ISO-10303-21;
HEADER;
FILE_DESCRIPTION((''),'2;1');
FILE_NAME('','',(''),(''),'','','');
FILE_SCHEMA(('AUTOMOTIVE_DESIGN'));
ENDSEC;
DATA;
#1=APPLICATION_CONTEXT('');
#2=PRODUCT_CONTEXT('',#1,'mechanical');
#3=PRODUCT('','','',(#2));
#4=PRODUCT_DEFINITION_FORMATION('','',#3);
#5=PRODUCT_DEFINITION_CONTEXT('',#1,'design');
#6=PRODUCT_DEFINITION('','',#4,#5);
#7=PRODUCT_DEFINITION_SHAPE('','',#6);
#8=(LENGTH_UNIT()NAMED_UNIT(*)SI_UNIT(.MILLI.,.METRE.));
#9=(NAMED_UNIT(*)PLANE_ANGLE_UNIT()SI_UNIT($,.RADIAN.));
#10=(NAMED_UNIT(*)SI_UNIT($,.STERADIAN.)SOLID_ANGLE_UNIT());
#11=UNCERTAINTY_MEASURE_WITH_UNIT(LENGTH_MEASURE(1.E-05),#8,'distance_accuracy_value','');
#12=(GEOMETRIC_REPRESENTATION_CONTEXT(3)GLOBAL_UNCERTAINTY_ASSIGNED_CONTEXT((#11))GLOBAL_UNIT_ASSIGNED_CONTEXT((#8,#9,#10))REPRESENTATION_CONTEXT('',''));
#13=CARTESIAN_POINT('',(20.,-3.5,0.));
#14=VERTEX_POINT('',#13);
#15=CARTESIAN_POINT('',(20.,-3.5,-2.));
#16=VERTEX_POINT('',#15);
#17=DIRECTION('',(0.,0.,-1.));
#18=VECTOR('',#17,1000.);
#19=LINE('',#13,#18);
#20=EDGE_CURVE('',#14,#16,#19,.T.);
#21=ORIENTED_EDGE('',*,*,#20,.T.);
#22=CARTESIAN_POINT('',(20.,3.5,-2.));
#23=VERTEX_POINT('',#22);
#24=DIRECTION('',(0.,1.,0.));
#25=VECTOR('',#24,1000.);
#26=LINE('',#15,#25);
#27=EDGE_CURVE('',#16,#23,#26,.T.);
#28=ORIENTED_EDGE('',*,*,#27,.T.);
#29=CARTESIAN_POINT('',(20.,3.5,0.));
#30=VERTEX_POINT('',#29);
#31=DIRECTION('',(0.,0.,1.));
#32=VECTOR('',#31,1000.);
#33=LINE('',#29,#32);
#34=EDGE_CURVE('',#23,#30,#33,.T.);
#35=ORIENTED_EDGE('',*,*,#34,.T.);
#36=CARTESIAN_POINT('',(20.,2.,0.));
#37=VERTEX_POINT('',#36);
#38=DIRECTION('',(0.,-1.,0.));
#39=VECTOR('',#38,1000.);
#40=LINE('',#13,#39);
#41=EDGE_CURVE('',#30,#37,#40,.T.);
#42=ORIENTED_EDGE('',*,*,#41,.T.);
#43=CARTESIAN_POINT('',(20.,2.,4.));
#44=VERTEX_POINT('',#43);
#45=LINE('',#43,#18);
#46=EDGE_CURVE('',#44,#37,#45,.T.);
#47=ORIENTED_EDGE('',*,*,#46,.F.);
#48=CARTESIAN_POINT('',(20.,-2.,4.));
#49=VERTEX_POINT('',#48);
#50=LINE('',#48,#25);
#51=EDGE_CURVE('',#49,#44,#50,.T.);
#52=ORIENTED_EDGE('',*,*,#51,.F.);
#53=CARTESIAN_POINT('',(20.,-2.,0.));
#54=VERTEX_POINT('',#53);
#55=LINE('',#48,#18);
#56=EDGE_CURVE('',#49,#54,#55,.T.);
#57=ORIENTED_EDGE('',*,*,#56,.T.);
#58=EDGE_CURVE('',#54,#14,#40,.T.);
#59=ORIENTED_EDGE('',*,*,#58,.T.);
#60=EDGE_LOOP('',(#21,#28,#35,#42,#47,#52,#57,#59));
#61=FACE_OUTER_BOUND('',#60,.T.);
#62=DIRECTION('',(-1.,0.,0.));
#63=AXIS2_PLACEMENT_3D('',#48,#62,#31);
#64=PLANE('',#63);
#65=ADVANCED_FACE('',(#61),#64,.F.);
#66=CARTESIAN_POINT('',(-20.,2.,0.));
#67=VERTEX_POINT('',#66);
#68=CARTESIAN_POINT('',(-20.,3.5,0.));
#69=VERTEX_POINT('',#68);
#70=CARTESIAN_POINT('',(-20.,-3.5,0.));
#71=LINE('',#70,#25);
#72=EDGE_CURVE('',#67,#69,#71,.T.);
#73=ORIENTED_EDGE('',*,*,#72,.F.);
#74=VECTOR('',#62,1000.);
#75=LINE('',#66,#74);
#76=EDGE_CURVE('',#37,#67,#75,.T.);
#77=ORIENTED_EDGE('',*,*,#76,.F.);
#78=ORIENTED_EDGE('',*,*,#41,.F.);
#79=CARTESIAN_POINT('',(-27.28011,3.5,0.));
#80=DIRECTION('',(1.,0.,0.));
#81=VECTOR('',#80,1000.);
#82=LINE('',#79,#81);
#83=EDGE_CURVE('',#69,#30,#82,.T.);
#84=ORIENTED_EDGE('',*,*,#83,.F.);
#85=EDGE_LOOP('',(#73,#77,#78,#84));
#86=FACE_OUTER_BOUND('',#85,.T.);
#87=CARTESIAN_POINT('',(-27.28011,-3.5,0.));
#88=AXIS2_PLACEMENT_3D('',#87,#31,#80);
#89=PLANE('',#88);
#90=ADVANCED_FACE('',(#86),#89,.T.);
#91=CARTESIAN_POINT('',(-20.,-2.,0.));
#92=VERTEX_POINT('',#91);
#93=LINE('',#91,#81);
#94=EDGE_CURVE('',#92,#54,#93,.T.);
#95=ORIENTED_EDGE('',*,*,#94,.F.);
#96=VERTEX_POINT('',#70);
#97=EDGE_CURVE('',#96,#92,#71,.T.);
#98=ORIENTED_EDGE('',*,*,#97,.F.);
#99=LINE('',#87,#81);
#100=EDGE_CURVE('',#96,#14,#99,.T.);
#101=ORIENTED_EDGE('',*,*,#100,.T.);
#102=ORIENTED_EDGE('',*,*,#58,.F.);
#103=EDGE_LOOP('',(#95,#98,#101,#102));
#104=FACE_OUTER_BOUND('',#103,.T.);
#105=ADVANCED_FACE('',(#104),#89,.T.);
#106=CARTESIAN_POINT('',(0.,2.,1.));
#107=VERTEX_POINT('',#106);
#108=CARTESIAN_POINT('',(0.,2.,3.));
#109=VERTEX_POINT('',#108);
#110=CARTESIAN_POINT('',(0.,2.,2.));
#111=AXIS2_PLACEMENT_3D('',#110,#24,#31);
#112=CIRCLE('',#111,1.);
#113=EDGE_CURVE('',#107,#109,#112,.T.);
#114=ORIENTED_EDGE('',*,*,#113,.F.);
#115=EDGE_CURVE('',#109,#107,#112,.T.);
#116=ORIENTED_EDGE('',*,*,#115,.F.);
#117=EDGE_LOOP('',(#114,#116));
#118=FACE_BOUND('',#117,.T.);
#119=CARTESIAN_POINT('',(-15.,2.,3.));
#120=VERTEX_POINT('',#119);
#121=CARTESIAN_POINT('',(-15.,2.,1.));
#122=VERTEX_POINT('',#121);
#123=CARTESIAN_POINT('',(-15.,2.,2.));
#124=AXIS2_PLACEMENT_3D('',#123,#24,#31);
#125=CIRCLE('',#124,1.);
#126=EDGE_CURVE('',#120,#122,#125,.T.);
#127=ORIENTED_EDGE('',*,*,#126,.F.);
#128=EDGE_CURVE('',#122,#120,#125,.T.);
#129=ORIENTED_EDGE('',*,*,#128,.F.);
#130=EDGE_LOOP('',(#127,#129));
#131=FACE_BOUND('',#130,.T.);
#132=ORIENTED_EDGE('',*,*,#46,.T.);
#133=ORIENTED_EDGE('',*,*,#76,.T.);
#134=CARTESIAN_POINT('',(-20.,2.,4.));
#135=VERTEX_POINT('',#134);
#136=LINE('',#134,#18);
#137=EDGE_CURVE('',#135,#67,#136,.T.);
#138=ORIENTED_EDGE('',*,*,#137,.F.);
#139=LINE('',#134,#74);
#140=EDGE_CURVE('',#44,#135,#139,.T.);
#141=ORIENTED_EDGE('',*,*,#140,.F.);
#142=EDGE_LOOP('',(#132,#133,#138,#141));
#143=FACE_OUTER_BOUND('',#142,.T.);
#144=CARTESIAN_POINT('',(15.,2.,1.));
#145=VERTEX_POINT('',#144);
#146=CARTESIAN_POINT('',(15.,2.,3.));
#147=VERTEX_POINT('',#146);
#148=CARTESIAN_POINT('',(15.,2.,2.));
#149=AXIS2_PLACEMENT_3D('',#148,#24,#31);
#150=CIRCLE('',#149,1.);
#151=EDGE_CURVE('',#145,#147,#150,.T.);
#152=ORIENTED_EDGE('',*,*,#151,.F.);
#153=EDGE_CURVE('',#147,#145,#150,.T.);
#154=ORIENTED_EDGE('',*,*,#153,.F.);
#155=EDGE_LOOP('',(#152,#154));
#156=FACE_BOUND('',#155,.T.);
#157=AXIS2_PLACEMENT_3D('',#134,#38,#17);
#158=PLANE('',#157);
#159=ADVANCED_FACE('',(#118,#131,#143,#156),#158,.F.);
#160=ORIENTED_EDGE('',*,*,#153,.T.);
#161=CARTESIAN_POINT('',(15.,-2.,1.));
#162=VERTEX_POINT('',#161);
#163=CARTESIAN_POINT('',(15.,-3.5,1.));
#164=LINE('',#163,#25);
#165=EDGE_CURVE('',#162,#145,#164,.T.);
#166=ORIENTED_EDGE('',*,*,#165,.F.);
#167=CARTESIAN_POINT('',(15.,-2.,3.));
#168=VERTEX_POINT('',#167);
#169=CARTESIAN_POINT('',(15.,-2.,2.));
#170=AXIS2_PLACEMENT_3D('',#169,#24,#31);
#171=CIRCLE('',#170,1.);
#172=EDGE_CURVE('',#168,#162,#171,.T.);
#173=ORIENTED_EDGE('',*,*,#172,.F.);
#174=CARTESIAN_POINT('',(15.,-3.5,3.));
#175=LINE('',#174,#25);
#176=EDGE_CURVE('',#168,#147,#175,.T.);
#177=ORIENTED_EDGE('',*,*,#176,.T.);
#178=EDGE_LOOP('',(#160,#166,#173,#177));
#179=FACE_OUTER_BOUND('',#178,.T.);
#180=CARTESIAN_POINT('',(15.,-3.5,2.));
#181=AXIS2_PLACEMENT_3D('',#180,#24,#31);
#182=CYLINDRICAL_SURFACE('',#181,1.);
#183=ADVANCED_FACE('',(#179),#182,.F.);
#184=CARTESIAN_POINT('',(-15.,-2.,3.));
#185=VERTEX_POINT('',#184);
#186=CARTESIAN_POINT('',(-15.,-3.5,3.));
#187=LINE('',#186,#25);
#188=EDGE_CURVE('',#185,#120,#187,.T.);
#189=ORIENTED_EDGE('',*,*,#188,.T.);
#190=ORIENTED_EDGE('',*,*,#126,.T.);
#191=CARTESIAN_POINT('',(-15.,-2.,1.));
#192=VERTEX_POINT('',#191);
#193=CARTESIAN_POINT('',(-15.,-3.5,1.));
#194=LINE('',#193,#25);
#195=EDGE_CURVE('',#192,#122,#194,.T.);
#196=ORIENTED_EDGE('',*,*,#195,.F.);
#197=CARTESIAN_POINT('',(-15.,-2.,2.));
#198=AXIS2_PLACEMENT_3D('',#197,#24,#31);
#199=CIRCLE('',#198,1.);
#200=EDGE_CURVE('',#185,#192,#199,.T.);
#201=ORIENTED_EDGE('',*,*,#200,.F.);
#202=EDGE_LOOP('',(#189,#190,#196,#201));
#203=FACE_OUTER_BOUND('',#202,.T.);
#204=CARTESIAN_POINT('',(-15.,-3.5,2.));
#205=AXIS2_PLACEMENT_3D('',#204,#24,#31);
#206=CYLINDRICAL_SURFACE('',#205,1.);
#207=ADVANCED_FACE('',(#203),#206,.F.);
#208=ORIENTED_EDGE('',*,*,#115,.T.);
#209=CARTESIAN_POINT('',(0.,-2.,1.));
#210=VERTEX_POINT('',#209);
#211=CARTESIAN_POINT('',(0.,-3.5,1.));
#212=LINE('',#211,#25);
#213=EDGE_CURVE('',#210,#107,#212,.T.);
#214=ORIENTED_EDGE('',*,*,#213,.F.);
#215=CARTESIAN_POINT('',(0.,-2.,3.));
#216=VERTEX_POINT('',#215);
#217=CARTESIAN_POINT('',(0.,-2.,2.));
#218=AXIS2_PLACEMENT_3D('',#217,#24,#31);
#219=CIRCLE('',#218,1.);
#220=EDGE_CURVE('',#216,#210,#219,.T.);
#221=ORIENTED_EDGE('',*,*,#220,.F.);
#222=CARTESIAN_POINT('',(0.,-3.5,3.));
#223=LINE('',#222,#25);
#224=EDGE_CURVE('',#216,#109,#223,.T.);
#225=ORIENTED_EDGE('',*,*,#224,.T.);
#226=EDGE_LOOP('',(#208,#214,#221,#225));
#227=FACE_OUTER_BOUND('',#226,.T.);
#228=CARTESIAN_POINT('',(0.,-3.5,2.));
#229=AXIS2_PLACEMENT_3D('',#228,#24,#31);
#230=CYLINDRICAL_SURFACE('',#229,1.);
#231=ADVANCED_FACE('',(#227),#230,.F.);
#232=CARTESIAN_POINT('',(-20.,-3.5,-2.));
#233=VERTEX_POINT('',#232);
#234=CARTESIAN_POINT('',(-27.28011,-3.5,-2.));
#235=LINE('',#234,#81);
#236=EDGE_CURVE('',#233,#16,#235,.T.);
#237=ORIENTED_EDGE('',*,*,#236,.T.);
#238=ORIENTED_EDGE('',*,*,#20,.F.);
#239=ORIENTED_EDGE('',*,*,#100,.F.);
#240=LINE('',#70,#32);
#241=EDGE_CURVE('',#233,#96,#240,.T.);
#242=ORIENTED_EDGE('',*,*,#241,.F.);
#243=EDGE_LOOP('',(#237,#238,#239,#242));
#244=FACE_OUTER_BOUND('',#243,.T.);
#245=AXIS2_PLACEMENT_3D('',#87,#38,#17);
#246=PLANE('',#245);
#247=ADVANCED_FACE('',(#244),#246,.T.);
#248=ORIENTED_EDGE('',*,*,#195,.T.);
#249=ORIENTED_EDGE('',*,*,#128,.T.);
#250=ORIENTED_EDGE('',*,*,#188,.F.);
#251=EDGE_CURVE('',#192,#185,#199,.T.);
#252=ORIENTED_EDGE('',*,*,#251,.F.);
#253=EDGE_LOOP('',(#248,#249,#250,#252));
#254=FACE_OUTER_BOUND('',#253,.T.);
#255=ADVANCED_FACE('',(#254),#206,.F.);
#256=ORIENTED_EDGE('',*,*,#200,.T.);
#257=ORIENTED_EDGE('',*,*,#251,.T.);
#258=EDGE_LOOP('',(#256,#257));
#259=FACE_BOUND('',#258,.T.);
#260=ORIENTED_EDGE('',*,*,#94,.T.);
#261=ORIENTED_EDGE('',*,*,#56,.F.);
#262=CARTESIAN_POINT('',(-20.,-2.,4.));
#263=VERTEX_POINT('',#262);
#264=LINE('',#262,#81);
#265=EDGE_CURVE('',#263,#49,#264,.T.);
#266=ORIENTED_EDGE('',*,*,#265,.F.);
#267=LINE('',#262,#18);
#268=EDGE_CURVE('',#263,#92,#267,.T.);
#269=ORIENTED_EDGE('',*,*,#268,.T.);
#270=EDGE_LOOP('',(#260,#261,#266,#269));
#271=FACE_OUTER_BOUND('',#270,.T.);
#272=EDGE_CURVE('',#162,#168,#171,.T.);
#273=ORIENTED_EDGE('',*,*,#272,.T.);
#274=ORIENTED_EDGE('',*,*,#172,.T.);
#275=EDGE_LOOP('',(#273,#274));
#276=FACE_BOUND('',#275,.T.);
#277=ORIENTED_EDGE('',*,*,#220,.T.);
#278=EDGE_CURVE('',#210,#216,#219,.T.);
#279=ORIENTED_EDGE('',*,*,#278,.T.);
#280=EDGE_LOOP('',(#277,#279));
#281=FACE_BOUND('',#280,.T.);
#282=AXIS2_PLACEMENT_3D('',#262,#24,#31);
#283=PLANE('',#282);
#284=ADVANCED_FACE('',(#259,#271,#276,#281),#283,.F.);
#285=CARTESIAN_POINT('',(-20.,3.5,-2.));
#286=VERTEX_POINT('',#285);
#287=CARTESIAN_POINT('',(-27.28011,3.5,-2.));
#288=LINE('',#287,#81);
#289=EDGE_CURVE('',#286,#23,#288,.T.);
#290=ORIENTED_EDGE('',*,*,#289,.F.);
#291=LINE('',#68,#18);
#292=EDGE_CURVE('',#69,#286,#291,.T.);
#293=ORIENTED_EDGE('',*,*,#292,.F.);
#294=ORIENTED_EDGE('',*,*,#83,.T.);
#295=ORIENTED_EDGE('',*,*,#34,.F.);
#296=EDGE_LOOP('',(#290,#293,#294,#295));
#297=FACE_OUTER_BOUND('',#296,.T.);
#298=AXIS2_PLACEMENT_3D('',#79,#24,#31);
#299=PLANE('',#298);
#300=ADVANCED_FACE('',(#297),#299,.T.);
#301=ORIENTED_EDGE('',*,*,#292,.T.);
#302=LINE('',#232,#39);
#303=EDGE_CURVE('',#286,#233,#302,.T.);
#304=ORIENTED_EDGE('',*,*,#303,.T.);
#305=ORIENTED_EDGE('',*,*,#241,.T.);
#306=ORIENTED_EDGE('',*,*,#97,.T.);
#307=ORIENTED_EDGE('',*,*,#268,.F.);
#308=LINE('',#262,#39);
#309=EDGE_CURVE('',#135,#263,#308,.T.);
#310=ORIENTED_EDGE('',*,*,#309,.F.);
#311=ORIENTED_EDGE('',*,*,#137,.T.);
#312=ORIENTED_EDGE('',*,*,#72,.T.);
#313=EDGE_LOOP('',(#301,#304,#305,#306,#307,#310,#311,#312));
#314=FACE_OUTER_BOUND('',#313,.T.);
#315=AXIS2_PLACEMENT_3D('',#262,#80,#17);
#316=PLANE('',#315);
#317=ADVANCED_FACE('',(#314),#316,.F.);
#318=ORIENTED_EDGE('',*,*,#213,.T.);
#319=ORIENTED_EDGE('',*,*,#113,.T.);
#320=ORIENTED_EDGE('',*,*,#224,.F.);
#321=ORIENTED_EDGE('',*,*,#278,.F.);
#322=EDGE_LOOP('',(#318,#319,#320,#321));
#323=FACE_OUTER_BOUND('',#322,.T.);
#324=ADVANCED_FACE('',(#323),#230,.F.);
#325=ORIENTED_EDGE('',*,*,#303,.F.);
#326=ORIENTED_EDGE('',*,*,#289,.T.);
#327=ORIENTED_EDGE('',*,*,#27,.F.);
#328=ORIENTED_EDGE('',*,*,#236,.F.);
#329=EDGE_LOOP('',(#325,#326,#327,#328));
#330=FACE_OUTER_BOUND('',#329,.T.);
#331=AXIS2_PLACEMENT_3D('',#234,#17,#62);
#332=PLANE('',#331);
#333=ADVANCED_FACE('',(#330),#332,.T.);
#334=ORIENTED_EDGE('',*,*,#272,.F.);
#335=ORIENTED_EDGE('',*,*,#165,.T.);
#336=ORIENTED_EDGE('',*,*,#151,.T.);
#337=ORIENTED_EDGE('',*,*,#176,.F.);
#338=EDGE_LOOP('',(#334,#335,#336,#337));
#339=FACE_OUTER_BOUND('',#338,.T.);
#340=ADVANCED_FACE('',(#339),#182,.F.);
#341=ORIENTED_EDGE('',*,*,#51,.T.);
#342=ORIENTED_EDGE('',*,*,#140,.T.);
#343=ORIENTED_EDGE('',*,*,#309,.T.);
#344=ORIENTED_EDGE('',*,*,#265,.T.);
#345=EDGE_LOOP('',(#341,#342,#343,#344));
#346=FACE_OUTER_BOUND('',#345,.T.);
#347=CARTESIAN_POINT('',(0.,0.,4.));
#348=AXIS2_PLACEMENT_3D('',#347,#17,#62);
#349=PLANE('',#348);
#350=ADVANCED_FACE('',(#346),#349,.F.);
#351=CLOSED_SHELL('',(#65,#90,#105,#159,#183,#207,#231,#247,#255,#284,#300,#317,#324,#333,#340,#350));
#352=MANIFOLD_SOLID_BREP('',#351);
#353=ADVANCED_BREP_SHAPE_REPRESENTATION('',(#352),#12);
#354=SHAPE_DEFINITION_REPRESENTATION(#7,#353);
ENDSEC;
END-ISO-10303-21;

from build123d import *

# Parameters (mm, degrees)
SKETCH_1_W          = 40
SKETCH_1_H          = 4
EXTRUDE_1_DEPTH     = 4
SKETCH_2_W          = 2
SKETCH_2_H          = 7
EXTRUDE_2_DEPTH     = 40
SKETCH_3_R          = 1
CUT_EXTRUDE_1_DEPTH = 22.124630174


with BuildPart() as part:
    # 草图1 → 凸台-拉伸1 (new body)
    with BuildSketch(Plane.XY):
        Rectangle(SKETCH_1_W, SKETCH_1_H)
    extrude(amount=EXTRUDE_1_DEPTH)

    # 草图2 → 凸台-拉伸2 (add)
    with BuildSketch(Plane(origin=(20, 0, 0), x_dir=(0, 0, -1), z_dir=(1, 0, 0))):
        with Locations((1, 0)):
            Rectangle(SKETCH_2_W, SKETCH_2_H)
    extrude(amount=-EXTRUDE_2_DEPTH)

    # 草图3 → 切除-拉伸1 (cut, through all)
    with BuildSketch(Plane(origin=(0, 2, 0), x_dir=(1, 0, 0), z_dir=(0, 1, 0))):
        with Locations(Location((-15, -2, 0), (0, 0, 270))):
            Circle(SKETCH_3_R)
        with Locations(Location((0, -2, 0), (0, 0, 270))):
            Circle(SKETCH_3_R)
        with Locations(Location((15, -2, 0), (0, 0, 270))):
            Circle(SKETCH_3_R)
    extrude(amount=-CUT_EXTRUDE_1_DEPTH, mode=Mode.SUBTRACT)


solid = part.part
